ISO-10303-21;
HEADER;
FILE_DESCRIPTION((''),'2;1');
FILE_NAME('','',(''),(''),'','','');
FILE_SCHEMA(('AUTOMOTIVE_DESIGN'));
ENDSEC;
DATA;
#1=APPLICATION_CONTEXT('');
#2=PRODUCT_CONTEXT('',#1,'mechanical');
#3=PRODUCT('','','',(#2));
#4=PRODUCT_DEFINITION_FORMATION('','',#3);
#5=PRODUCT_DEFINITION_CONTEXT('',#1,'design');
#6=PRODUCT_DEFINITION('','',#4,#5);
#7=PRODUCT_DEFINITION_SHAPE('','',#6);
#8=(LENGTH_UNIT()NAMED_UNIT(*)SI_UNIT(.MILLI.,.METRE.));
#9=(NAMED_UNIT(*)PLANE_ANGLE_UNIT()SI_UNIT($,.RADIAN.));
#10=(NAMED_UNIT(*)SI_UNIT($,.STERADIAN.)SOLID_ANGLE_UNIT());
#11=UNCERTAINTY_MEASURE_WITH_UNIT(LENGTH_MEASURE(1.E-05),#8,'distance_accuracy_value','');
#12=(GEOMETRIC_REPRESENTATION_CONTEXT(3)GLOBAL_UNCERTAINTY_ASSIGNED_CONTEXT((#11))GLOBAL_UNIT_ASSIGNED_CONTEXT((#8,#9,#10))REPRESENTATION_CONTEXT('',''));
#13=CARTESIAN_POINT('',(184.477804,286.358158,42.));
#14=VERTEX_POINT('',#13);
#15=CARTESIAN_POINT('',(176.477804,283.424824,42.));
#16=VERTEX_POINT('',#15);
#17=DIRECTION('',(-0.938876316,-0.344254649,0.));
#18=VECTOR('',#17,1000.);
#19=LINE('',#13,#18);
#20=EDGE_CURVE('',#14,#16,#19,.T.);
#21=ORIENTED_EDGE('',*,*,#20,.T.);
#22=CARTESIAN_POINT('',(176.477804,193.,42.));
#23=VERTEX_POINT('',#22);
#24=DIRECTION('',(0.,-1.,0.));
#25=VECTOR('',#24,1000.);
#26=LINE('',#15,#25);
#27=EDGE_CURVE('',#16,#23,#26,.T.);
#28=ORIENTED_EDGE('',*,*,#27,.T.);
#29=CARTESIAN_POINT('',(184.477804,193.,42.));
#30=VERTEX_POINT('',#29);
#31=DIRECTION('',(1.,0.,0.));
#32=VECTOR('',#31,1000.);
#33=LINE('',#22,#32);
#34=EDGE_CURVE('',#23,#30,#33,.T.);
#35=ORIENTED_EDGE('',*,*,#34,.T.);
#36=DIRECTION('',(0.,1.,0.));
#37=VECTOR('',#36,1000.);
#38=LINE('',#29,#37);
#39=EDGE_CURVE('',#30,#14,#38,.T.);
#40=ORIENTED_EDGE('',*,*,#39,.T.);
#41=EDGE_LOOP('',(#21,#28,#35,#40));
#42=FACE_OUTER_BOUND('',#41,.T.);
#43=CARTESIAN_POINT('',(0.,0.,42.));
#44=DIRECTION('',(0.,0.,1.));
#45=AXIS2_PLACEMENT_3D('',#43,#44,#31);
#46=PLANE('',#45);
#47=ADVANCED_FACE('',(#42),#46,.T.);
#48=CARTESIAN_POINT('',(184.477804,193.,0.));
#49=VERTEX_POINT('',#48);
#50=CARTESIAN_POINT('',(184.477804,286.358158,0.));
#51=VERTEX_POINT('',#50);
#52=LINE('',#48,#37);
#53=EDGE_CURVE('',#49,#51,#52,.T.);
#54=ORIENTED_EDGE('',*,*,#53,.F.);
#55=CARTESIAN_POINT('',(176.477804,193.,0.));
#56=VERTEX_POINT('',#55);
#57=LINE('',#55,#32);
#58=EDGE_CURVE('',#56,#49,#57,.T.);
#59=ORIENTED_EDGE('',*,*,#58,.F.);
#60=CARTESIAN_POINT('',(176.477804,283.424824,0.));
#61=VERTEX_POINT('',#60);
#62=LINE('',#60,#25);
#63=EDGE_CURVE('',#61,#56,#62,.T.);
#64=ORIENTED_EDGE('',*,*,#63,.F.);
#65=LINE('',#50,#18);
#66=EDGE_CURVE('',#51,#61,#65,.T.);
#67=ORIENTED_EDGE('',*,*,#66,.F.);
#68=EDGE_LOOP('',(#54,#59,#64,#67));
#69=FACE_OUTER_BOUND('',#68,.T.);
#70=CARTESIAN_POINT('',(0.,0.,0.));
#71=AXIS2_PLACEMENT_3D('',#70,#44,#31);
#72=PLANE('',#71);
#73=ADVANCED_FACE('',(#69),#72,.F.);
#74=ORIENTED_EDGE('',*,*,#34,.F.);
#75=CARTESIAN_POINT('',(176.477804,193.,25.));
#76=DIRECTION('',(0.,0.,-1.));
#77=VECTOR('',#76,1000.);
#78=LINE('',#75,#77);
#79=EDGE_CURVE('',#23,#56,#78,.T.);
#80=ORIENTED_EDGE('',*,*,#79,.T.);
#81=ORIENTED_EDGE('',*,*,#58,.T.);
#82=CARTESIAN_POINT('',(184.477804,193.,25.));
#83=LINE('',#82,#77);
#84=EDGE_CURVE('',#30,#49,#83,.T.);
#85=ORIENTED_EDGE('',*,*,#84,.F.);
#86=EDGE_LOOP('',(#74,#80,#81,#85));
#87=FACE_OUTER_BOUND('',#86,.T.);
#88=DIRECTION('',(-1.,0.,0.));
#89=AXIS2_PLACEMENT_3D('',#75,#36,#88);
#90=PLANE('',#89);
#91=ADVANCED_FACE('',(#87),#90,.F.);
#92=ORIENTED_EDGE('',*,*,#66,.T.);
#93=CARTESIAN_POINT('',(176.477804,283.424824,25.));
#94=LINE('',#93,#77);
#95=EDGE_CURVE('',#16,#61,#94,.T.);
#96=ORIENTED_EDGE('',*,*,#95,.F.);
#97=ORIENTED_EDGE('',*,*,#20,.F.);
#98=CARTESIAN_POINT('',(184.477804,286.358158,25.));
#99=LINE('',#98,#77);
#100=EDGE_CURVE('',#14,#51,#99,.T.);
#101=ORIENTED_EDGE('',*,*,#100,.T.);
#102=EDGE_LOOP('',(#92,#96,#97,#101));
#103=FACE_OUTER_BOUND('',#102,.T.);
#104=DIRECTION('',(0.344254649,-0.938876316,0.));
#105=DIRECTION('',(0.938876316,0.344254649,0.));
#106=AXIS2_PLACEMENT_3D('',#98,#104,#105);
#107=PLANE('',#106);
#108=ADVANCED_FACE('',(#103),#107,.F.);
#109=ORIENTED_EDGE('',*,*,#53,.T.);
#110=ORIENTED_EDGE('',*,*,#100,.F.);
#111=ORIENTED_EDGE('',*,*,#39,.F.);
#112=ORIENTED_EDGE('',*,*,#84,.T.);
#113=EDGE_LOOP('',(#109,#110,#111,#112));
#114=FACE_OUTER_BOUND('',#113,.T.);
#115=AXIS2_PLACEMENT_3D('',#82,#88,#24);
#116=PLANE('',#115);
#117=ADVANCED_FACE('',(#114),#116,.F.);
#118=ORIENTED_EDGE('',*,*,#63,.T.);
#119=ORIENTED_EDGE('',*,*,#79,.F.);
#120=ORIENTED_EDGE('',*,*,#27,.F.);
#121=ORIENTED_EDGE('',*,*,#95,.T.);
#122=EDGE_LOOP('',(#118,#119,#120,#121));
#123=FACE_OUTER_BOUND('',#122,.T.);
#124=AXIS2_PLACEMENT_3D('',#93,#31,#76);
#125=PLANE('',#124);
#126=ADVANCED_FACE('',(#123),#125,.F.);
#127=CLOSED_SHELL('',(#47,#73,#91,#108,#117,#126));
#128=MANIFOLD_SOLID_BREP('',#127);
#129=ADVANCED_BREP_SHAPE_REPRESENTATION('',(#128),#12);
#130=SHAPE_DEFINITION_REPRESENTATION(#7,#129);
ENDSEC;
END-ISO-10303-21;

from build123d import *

# Parameters (mm, degrees)
EXTRUDE_1_DEPTH = 25
EXTRUDE_2_DEPTH = 17


with BuildPart() as part:
    # 草图1 → 凸台-拉伸1 (new body)
    with BuildSketch(Plane.XY):
        Polygon((176.477803528, 193), (184.477803528, 193), (184.477803528, 286.35815759), (176.477803528, 283.424824257), align=None)
    extrude(amount=EXTRUDE_1_DEPTH)

    # 草图2 → 凸台-拉伸2 (add)
    with BuildSketch(Plane.XY.offset(25)):
        Polygon((176.477803528, 283.424824257), (176.477803528, 193), (184.477803528, 193), (184.477803528, 286.35815759), align=None)
    extrude(amount=EXTRUDE_2_DEPTH)


solid = part.part
